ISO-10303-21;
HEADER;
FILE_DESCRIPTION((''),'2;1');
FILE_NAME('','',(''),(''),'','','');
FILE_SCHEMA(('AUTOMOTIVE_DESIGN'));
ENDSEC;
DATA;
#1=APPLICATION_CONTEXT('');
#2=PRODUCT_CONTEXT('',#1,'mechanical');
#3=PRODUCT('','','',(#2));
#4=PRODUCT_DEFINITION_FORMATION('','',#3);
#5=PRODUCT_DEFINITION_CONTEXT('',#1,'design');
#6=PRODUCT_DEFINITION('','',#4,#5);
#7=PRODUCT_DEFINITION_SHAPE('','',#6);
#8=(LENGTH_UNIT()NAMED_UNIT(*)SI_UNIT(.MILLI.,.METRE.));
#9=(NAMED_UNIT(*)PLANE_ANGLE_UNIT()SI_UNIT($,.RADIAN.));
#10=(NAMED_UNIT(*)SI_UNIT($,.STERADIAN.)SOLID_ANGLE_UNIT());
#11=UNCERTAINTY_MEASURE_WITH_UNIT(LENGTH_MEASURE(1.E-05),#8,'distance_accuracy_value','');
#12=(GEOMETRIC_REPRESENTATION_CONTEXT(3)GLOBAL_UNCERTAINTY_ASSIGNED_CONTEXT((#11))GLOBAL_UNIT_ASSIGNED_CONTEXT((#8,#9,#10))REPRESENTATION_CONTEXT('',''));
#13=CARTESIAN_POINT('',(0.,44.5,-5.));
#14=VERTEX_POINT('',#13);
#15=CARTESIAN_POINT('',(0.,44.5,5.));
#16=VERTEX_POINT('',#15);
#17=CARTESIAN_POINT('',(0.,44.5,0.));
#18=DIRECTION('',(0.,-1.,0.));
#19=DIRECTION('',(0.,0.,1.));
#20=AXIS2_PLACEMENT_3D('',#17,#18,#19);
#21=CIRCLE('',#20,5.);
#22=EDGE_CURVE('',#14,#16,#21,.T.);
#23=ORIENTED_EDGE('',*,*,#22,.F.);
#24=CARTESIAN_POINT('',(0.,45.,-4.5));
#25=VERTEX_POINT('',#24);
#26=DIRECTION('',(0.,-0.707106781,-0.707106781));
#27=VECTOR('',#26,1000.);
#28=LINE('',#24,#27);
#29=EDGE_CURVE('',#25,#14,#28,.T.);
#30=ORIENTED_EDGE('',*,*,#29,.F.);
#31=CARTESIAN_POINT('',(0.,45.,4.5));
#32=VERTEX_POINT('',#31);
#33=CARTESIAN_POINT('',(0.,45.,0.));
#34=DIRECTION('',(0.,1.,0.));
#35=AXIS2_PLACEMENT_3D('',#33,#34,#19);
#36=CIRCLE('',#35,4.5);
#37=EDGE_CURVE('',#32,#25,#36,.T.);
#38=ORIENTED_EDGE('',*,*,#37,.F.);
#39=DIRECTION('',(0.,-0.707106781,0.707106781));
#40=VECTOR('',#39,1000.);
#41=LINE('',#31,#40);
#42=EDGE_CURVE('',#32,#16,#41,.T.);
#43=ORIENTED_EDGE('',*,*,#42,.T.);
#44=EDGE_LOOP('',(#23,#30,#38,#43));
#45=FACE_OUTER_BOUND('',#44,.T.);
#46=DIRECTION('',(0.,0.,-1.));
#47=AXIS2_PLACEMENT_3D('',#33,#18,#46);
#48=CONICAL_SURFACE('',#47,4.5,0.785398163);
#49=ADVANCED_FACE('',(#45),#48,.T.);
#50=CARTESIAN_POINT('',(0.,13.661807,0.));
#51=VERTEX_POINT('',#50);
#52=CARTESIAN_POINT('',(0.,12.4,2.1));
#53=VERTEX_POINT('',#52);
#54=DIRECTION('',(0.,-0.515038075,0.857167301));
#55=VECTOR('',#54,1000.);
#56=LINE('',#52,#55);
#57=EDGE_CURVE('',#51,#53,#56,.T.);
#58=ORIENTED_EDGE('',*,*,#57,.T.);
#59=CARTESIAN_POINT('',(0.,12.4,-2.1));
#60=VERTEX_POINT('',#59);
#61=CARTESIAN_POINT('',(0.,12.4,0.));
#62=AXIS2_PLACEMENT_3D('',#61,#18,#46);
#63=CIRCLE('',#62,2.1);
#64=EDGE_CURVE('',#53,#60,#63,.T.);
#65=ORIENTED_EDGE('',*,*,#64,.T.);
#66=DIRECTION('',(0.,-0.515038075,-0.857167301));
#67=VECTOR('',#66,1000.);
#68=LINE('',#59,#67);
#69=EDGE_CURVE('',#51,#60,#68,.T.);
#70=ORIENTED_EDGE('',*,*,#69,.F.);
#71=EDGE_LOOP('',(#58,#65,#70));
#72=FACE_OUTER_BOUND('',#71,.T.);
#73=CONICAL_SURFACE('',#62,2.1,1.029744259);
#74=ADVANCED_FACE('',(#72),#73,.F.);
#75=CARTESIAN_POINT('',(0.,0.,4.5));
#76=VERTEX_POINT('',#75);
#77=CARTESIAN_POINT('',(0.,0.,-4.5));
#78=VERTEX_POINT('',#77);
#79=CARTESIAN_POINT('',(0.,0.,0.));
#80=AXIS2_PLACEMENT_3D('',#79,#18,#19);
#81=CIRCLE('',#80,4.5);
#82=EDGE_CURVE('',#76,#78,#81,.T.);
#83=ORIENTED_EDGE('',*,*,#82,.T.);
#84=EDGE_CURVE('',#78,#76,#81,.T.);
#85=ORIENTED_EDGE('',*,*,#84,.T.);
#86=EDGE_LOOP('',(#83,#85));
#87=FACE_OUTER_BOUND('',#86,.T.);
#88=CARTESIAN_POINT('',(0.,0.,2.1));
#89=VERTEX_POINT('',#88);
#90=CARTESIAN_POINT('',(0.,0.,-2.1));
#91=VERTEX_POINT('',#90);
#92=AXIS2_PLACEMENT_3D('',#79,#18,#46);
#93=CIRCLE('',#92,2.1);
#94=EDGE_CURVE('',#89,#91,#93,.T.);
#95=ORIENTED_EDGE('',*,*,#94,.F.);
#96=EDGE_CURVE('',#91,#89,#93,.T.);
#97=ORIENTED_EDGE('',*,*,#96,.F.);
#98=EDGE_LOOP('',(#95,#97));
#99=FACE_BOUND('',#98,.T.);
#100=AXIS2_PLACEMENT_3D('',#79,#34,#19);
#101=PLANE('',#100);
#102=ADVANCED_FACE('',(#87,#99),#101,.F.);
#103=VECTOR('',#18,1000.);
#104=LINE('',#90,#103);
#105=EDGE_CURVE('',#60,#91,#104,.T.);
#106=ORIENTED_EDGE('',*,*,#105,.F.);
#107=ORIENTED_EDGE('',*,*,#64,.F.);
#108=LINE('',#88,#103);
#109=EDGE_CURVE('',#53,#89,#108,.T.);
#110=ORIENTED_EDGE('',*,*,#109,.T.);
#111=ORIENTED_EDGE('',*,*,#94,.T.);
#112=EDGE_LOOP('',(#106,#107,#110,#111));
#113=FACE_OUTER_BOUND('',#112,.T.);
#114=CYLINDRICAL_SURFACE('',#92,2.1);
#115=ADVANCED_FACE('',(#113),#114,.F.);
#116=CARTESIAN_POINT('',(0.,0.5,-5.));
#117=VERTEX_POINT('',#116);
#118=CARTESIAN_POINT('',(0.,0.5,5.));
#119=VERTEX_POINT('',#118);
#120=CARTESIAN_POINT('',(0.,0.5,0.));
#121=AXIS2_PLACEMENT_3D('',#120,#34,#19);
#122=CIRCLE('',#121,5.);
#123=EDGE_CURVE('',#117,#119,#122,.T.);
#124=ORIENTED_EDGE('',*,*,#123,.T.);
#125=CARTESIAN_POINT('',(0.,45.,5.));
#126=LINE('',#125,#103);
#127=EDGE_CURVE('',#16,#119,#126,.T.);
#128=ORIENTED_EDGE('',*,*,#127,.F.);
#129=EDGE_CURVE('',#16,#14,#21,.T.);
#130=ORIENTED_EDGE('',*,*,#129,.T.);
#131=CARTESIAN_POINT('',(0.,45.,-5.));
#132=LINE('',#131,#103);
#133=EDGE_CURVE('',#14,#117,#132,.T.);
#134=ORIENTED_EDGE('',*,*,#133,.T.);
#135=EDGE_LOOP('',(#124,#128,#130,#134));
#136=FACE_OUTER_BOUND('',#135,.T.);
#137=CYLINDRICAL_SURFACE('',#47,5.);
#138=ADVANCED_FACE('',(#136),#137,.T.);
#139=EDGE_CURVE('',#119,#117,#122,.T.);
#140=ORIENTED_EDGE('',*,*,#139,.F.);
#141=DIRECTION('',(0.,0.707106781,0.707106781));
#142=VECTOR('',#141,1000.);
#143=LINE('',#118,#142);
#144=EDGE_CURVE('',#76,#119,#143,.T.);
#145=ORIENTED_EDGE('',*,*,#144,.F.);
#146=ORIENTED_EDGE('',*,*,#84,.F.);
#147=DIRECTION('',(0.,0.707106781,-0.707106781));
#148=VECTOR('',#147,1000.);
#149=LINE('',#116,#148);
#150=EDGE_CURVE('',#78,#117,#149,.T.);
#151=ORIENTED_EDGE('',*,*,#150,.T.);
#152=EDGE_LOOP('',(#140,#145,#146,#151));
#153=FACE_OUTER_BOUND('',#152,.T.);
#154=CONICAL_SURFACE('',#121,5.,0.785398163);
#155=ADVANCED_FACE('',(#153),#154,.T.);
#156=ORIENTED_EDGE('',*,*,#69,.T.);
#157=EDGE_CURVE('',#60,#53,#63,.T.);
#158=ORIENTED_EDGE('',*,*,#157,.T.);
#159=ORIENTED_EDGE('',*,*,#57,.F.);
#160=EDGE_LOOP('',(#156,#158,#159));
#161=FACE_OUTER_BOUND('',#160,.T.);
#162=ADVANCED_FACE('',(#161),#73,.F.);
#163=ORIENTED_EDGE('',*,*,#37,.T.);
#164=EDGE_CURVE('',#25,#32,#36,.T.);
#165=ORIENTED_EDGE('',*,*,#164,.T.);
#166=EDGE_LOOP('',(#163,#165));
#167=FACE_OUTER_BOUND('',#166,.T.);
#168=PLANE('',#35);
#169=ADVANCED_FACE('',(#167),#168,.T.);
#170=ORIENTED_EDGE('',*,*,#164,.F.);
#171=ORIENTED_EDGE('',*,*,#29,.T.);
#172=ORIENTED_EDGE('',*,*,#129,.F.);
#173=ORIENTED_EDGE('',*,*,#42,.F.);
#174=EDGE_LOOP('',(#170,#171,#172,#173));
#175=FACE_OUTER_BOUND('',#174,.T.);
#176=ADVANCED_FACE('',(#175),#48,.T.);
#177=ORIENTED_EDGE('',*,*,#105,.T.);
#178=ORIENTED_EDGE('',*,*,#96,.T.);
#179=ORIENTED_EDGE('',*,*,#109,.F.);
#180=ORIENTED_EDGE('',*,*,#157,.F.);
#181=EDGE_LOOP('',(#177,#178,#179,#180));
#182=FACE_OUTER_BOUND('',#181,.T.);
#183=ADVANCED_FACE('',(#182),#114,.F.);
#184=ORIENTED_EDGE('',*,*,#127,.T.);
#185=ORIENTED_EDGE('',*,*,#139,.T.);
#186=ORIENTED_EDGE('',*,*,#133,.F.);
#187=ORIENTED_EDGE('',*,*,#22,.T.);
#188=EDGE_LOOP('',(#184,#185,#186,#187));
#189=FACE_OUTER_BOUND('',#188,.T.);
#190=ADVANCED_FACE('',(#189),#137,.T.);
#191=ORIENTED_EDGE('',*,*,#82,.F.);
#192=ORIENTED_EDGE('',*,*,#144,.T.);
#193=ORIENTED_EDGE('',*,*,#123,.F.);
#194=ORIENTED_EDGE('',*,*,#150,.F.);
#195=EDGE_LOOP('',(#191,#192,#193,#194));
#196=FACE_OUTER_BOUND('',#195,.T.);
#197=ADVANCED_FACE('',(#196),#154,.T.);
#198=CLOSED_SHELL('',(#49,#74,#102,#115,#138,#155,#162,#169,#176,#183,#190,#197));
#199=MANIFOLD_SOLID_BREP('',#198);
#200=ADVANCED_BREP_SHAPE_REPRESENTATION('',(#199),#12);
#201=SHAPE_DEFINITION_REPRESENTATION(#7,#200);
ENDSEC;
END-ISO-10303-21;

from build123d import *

# Parameters (mm, degrees)
SKETCH1_R             = 5
BOSS_EXTRUDE1_DEPTH   = 45
M5_TAPPED_HOLE1_D     = 4.2
M5_TAPPED_HOLE1_DEPTH = 12.4
M5_TAPPED_HOLE1_TIP   = 1.2618073
CHAMFER1_SIZE         = 0.5


with BuildPart() as part:
    # Sketch1 → Boss-Extrude1 (new body)
    with BuildSketch(Plane(origin=(0, 0, 0), x_dir=(1, 0, 0), z_dir=(0, 1, 0))):
        with Locations(Location((0, 0, 0), (0, 0, 90))):
            Circle(SKETCH1_R)
    extrude(amount=BOSS_EXTRUDE1_DEPTH)

    # M5 Tapped Hole1
    with Locations(Plane(origin=(0, 0, 0), x_dir=(0, 0, -1), z_dir=(0, -1, 0))):
        with Locations((0, 0)):
            Hole(M5_TAPPED_HOLE1_D / 2, depth=M5_TAPPED_HOLE1_DEPTH)
            with Locations((0, 0, -(M5_TAPPED_HOLE1_DEPTH + M5_TAPPED_HOLE1_TIP / 2))):  # 118° drill point
                Cone(0, M5_TAPPED_HOLE1_D / 2, M5_TAPPED_HOLE1_TIP, mode=Mode.SUBTRACT)

    # Chamfer1
    chamfer1_edges = [part.edges().sort_by_distance(p)[0] for p in [
        (0, 0, 5),
        (0, 45, 5),
    ]]
    chamfer(chamfer1_edges, length=CHAMFER1_SIZE)


solid = part.part
